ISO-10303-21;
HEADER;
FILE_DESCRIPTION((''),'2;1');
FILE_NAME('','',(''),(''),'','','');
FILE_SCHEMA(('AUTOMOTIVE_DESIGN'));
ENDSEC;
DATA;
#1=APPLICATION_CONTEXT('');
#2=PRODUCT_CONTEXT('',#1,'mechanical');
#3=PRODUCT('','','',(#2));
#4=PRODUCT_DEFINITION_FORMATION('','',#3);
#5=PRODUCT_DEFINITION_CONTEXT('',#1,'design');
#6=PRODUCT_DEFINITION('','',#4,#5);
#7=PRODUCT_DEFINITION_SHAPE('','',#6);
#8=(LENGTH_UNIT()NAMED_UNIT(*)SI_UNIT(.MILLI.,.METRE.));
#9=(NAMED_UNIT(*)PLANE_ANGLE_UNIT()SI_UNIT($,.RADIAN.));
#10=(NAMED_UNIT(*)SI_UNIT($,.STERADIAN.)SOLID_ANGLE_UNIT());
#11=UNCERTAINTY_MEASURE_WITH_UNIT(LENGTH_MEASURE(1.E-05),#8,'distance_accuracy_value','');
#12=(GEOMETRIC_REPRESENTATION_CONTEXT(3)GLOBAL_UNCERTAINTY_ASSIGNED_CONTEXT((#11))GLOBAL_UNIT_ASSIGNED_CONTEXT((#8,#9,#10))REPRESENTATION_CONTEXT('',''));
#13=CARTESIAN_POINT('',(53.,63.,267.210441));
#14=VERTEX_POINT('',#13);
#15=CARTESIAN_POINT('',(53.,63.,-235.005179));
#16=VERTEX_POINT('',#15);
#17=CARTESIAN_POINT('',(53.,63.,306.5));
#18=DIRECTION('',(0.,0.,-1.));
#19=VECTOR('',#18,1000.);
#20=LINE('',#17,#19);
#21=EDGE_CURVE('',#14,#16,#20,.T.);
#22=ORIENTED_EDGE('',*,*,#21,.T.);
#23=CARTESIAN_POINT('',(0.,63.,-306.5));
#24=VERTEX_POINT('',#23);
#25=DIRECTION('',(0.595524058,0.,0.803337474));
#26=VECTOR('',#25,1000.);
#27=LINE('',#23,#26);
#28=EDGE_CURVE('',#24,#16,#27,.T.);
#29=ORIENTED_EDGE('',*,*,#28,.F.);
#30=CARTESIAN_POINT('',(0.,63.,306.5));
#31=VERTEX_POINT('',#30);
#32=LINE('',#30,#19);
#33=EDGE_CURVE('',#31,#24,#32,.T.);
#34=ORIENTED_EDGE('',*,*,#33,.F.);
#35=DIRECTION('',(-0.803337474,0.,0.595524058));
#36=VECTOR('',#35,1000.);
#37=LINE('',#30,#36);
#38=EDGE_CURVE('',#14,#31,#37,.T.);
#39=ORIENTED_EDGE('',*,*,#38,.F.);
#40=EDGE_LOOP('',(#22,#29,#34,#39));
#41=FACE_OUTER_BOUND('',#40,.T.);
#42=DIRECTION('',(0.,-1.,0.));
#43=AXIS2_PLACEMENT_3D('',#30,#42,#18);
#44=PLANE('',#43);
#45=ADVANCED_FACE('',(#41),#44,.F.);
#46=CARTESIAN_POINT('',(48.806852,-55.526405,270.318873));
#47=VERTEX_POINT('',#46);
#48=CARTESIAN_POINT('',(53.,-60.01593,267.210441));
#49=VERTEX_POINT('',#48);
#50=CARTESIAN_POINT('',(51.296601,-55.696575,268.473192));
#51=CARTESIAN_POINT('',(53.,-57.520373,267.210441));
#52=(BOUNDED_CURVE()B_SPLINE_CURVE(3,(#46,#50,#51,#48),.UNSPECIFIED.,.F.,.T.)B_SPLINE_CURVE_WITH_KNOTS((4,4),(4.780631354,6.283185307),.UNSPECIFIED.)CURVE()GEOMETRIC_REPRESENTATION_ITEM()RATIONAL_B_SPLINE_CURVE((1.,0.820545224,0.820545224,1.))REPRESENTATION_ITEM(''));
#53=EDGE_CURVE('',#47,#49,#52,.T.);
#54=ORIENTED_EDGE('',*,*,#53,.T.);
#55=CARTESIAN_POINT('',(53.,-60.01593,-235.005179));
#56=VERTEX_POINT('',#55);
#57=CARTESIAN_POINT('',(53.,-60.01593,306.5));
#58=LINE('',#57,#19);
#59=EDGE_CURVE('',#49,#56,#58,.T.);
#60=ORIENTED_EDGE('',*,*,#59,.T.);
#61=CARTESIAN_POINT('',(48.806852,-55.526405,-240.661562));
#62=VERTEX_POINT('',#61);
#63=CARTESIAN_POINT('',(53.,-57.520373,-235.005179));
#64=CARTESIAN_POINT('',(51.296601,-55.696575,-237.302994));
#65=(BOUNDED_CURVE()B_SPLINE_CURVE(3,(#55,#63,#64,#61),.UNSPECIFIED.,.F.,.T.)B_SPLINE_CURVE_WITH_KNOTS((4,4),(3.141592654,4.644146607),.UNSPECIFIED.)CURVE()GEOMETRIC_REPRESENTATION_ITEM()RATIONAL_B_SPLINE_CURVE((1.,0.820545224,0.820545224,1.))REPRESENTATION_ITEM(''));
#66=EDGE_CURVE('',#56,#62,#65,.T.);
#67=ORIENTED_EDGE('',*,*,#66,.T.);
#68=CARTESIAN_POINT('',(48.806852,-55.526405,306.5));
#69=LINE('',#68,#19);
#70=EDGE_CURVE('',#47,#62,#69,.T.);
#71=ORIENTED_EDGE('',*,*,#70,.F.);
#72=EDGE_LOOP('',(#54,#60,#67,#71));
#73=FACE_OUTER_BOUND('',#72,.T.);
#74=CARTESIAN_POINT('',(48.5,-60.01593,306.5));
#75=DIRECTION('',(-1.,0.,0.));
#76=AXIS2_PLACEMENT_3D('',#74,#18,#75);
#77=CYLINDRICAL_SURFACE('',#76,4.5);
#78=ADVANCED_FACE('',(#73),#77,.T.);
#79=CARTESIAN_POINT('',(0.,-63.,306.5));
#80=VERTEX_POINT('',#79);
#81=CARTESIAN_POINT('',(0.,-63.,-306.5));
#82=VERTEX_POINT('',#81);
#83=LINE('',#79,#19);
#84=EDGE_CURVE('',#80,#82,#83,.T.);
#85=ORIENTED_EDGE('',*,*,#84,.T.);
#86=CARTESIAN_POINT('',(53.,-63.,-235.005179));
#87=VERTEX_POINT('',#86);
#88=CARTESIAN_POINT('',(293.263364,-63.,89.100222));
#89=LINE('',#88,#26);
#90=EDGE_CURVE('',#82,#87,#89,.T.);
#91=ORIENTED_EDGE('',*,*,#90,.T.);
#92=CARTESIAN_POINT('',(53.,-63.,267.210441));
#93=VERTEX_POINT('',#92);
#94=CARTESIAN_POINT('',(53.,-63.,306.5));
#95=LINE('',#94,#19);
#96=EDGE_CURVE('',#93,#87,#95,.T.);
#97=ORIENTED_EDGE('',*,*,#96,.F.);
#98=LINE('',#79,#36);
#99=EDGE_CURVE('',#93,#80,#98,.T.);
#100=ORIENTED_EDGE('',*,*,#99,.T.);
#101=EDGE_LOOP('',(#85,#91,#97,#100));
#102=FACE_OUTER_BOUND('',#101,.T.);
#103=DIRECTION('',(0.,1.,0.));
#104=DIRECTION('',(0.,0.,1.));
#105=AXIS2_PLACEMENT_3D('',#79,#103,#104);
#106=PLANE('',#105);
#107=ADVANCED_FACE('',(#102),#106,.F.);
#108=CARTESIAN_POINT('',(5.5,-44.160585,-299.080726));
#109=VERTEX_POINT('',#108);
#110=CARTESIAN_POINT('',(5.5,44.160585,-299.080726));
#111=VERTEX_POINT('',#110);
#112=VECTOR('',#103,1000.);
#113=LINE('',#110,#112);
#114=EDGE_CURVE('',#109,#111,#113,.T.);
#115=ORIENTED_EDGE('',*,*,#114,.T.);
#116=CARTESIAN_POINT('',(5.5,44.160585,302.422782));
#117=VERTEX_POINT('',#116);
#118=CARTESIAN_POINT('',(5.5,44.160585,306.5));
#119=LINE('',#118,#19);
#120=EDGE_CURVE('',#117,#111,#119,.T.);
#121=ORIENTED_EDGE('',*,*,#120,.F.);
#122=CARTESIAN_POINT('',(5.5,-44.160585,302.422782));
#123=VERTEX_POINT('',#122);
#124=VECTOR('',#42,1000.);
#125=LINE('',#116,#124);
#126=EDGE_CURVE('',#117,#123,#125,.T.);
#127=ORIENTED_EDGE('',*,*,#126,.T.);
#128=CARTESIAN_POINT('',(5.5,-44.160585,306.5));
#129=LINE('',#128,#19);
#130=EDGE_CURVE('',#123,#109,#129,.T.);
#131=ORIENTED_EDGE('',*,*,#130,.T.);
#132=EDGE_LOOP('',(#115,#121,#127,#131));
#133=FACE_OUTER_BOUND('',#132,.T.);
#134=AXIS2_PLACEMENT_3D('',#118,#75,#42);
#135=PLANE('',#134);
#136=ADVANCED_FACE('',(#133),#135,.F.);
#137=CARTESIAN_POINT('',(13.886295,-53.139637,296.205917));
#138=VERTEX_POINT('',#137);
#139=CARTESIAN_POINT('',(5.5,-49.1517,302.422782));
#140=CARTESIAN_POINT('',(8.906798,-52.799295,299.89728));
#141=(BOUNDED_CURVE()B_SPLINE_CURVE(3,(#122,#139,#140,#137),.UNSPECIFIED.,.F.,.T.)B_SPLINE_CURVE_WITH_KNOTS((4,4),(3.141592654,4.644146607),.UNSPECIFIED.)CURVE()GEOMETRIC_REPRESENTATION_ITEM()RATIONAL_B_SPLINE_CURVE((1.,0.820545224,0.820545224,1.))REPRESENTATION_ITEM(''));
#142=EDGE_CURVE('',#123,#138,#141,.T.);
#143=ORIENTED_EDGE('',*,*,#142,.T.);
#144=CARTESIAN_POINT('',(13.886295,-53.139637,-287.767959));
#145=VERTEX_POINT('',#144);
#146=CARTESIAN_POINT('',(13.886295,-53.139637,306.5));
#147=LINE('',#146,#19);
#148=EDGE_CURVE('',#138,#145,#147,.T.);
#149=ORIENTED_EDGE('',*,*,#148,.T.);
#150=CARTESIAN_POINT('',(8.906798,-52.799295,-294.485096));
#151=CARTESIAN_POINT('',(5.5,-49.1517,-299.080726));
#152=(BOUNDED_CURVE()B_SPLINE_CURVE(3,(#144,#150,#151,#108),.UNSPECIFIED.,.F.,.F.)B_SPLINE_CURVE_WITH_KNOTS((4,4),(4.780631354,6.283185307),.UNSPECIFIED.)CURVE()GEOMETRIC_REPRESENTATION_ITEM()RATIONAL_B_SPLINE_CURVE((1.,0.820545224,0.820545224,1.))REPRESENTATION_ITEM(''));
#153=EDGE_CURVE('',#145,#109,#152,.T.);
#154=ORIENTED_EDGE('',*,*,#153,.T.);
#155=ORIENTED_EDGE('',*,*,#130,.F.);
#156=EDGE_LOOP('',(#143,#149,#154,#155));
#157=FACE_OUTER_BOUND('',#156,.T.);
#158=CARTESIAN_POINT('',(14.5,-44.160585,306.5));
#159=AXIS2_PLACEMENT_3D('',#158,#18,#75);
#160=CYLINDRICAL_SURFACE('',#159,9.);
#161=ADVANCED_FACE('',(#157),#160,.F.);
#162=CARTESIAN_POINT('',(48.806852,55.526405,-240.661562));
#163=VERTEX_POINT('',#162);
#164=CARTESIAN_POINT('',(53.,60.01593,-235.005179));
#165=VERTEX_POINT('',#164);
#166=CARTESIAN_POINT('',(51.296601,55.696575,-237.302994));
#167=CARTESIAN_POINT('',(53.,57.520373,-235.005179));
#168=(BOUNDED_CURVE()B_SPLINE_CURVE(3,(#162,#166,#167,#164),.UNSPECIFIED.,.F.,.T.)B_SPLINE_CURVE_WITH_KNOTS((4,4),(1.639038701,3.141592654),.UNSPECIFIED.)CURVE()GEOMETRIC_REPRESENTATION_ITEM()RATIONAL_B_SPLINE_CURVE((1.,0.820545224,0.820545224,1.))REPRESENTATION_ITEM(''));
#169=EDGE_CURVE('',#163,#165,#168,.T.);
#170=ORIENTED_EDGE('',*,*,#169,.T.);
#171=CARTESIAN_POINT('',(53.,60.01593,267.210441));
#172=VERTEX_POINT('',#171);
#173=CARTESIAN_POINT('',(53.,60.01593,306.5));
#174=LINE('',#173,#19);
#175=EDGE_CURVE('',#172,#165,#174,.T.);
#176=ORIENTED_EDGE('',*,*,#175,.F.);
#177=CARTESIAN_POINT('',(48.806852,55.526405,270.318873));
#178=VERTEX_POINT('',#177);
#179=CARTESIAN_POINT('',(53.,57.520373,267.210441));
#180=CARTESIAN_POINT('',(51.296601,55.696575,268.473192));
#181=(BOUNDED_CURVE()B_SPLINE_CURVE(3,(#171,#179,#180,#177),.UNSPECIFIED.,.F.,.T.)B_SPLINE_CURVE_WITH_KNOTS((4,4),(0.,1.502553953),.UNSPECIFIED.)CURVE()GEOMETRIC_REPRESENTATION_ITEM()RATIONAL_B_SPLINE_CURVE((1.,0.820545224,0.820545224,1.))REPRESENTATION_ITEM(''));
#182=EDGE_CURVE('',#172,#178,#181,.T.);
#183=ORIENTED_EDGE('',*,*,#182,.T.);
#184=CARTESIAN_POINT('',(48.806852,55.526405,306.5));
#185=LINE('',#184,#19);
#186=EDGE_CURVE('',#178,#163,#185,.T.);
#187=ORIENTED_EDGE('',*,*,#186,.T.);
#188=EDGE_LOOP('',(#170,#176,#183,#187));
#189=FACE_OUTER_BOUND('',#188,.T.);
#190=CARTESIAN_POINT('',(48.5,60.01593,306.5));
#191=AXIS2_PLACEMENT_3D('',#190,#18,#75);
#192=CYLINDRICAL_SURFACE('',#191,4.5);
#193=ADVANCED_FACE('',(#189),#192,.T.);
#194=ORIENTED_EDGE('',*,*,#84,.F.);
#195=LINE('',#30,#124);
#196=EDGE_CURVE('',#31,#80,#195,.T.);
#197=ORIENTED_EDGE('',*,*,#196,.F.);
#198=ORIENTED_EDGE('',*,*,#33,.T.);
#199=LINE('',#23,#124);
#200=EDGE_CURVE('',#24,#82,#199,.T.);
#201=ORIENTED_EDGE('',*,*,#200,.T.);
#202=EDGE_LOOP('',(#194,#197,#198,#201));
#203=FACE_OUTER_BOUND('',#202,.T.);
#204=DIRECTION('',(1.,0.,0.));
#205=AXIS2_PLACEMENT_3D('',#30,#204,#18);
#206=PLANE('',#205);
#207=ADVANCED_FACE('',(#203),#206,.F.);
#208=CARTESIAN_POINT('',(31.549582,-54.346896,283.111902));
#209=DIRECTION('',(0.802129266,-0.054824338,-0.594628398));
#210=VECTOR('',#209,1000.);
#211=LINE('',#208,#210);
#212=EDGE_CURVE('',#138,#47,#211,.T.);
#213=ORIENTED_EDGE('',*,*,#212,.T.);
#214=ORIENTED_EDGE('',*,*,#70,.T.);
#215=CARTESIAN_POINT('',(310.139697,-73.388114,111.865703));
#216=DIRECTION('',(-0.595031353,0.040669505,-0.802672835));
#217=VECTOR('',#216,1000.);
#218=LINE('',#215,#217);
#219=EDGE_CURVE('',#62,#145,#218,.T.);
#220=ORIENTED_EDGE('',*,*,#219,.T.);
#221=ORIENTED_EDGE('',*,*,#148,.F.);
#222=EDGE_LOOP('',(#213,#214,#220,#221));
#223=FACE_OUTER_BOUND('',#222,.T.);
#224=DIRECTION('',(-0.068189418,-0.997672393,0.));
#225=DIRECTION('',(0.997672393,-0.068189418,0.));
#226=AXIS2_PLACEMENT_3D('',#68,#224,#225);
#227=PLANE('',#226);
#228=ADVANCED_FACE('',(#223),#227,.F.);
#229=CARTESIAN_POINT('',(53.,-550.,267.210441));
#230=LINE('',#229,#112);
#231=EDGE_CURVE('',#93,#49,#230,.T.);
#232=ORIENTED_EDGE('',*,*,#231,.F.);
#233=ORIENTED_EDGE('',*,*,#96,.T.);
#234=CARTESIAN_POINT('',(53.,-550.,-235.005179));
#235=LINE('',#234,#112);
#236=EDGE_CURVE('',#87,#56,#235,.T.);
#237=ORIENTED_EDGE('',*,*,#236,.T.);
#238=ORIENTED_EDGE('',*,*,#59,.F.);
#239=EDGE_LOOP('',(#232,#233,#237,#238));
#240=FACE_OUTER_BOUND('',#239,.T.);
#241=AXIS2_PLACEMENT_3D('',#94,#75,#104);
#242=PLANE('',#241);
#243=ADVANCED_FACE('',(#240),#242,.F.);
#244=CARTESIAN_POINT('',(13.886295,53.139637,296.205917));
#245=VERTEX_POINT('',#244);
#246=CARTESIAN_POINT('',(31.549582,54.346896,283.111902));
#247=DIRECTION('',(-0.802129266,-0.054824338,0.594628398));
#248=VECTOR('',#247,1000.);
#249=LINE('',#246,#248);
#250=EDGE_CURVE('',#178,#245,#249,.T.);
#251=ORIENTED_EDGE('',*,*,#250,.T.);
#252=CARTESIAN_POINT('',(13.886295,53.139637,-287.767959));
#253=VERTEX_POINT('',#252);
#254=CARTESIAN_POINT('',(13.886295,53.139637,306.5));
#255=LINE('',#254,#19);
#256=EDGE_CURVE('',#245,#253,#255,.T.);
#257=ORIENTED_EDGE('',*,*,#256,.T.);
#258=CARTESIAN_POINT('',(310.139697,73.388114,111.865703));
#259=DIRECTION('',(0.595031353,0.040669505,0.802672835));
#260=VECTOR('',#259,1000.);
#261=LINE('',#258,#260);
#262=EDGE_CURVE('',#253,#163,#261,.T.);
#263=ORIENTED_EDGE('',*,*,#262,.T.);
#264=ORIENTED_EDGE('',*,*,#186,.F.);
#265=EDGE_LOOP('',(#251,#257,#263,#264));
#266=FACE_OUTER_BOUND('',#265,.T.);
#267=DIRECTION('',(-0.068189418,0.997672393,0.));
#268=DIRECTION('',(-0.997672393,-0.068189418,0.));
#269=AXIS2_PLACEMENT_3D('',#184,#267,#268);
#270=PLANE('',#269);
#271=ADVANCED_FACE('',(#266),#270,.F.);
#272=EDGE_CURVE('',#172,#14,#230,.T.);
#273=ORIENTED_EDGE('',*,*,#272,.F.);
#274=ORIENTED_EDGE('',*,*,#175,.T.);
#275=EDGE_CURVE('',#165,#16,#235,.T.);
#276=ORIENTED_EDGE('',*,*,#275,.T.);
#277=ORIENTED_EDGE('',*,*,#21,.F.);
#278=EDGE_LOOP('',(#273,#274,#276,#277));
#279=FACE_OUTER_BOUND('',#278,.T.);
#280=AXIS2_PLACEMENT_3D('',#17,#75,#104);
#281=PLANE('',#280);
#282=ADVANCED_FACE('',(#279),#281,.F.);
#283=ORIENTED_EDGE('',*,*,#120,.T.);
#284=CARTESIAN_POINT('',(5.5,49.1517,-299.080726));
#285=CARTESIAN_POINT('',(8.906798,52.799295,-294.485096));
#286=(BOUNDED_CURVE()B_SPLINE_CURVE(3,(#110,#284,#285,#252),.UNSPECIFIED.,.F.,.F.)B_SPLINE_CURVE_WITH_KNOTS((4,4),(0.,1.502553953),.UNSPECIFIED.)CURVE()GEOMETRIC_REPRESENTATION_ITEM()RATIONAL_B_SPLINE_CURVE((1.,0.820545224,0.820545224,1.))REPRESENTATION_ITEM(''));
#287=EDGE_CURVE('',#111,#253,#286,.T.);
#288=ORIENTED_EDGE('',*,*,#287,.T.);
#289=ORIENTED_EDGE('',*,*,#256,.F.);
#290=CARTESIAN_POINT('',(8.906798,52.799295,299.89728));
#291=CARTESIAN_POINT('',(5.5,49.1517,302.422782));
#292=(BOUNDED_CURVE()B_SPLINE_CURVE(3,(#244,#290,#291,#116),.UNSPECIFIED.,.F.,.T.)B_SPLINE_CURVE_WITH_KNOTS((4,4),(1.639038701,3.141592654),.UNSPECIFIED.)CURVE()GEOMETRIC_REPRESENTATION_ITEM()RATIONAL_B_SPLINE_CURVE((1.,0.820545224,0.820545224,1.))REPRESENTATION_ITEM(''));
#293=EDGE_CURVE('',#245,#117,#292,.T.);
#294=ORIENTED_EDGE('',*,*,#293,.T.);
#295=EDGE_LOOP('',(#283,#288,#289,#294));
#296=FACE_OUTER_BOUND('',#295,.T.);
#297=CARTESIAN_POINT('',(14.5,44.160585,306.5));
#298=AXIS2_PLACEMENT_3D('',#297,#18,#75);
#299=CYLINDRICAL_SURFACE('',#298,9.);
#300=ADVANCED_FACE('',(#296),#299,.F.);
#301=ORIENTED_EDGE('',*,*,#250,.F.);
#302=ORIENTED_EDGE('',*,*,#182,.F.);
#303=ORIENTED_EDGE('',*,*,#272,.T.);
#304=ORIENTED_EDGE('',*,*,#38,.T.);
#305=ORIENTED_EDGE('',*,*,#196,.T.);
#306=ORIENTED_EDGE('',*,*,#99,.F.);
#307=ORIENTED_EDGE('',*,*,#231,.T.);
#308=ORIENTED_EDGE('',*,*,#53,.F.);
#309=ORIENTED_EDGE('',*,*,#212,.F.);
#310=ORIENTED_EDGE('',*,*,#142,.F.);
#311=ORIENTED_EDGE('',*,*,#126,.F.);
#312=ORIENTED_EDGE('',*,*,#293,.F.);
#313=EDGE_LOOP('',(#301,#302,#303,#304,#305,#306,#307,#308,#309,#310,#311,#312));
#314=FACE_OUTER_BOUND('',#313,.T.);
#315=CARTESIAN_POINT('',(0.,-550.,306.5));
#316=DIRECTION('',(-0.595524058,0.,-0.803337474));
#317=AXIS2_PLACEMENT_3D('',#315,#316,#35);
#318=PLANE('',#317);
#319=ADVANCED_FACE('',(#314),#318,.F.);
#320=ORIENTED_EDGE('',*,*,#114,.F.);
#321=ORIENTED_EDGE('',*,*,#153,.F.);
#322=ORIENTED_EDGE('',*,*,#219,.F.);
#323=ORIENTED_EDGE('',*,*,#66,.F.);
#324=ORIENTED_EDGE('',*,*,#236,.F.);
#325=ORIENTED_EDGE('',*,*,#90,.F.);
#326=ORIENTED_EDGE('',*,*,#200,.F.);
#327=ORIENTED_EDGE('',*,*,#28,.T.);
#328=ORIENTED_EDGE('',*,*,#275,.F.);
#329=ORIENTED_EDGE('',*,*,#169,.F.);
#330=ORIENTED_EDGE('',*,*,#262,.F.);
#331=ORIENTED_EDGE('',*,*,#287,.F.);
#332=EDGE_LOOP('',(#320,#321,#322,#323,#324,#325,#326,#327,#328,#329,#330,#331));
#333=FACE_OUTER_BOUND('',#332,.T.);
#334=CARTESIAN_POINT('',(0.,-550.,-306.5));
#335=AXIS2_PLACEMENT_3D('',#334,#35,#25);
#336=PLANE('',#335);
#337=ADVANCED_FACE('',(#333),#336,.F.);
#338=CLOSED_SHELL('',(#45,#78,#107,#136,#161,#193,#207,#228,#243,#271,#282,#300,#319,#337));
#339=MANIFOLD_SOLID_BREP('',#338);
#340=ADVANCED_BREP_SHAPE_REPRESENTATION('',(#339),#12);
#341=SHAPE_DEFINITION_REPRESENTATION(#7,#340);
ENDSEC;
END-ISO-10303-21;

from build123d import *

# Parameters (mm, degrees)
BOSS_EXTRUDE1_DEPTH = 306.5
CUT_EXTRUDE1_DEPTH  = 613


with BuildPart() as part:
    # Sketch1 → Boss-Extrude1 (new, symmetric)
    with BuildSketch(Plane.XY):
        with BuildLine():
            Line((0, 63), (0, -63))
            Line((0, -63), (53, -63))
            Line((53, -63), (53, -60.015930389))
            ThreePointArc((53, -60.015930389), (51.788680261, -56.944353898), (48.806852383, -55.526404621))
            Line((48.806852383, -55.526404621), (13.886295235, -53.139636681))
            ThreePointArc((13.886295235, -53.139636681), (7.922639477, -50.303738128), (5.5, -44.160585147))
            Line((5.5, -44.160585147), (5.5, 44.160585147))
            ThreePointArc((5.5, 44.160585147), (7.922639477, 50.303738128), (13.886295235, 53.139636681))
            Line((13.886295235, 53.139636681), (48.806852383, 55.526404621))
            ThreePointArc((48.806852383, 55.526404621), (51.788680261, 56.944353898), (53, 60.015930389))
            Line((53, 60.015930389), (53, 63))
            Line((53, 63), (0, 63))
        make_face()
    extrude(amount=BOSS_EXTRUDE1_DEPTH, both=True)

    # Sketch2 → Cut-Extrude1 (cut)
    with BuildSketch(Plane(origin=(0, 63, 0), x_dir=(1, 0, 0), z_dir=(0, 1, 0))):
        Polygon((0, -306.5), (53, -267.210441025), (53, -306.5), align=None)
        Polygon((0, 306.5), (53, 235.005178647), (53, 306.5), align=None)
    extrude(amount=-CUT_EXTRUDE1_DEPTH, mode=Mode.SUBTRACT)


solid = part.part
